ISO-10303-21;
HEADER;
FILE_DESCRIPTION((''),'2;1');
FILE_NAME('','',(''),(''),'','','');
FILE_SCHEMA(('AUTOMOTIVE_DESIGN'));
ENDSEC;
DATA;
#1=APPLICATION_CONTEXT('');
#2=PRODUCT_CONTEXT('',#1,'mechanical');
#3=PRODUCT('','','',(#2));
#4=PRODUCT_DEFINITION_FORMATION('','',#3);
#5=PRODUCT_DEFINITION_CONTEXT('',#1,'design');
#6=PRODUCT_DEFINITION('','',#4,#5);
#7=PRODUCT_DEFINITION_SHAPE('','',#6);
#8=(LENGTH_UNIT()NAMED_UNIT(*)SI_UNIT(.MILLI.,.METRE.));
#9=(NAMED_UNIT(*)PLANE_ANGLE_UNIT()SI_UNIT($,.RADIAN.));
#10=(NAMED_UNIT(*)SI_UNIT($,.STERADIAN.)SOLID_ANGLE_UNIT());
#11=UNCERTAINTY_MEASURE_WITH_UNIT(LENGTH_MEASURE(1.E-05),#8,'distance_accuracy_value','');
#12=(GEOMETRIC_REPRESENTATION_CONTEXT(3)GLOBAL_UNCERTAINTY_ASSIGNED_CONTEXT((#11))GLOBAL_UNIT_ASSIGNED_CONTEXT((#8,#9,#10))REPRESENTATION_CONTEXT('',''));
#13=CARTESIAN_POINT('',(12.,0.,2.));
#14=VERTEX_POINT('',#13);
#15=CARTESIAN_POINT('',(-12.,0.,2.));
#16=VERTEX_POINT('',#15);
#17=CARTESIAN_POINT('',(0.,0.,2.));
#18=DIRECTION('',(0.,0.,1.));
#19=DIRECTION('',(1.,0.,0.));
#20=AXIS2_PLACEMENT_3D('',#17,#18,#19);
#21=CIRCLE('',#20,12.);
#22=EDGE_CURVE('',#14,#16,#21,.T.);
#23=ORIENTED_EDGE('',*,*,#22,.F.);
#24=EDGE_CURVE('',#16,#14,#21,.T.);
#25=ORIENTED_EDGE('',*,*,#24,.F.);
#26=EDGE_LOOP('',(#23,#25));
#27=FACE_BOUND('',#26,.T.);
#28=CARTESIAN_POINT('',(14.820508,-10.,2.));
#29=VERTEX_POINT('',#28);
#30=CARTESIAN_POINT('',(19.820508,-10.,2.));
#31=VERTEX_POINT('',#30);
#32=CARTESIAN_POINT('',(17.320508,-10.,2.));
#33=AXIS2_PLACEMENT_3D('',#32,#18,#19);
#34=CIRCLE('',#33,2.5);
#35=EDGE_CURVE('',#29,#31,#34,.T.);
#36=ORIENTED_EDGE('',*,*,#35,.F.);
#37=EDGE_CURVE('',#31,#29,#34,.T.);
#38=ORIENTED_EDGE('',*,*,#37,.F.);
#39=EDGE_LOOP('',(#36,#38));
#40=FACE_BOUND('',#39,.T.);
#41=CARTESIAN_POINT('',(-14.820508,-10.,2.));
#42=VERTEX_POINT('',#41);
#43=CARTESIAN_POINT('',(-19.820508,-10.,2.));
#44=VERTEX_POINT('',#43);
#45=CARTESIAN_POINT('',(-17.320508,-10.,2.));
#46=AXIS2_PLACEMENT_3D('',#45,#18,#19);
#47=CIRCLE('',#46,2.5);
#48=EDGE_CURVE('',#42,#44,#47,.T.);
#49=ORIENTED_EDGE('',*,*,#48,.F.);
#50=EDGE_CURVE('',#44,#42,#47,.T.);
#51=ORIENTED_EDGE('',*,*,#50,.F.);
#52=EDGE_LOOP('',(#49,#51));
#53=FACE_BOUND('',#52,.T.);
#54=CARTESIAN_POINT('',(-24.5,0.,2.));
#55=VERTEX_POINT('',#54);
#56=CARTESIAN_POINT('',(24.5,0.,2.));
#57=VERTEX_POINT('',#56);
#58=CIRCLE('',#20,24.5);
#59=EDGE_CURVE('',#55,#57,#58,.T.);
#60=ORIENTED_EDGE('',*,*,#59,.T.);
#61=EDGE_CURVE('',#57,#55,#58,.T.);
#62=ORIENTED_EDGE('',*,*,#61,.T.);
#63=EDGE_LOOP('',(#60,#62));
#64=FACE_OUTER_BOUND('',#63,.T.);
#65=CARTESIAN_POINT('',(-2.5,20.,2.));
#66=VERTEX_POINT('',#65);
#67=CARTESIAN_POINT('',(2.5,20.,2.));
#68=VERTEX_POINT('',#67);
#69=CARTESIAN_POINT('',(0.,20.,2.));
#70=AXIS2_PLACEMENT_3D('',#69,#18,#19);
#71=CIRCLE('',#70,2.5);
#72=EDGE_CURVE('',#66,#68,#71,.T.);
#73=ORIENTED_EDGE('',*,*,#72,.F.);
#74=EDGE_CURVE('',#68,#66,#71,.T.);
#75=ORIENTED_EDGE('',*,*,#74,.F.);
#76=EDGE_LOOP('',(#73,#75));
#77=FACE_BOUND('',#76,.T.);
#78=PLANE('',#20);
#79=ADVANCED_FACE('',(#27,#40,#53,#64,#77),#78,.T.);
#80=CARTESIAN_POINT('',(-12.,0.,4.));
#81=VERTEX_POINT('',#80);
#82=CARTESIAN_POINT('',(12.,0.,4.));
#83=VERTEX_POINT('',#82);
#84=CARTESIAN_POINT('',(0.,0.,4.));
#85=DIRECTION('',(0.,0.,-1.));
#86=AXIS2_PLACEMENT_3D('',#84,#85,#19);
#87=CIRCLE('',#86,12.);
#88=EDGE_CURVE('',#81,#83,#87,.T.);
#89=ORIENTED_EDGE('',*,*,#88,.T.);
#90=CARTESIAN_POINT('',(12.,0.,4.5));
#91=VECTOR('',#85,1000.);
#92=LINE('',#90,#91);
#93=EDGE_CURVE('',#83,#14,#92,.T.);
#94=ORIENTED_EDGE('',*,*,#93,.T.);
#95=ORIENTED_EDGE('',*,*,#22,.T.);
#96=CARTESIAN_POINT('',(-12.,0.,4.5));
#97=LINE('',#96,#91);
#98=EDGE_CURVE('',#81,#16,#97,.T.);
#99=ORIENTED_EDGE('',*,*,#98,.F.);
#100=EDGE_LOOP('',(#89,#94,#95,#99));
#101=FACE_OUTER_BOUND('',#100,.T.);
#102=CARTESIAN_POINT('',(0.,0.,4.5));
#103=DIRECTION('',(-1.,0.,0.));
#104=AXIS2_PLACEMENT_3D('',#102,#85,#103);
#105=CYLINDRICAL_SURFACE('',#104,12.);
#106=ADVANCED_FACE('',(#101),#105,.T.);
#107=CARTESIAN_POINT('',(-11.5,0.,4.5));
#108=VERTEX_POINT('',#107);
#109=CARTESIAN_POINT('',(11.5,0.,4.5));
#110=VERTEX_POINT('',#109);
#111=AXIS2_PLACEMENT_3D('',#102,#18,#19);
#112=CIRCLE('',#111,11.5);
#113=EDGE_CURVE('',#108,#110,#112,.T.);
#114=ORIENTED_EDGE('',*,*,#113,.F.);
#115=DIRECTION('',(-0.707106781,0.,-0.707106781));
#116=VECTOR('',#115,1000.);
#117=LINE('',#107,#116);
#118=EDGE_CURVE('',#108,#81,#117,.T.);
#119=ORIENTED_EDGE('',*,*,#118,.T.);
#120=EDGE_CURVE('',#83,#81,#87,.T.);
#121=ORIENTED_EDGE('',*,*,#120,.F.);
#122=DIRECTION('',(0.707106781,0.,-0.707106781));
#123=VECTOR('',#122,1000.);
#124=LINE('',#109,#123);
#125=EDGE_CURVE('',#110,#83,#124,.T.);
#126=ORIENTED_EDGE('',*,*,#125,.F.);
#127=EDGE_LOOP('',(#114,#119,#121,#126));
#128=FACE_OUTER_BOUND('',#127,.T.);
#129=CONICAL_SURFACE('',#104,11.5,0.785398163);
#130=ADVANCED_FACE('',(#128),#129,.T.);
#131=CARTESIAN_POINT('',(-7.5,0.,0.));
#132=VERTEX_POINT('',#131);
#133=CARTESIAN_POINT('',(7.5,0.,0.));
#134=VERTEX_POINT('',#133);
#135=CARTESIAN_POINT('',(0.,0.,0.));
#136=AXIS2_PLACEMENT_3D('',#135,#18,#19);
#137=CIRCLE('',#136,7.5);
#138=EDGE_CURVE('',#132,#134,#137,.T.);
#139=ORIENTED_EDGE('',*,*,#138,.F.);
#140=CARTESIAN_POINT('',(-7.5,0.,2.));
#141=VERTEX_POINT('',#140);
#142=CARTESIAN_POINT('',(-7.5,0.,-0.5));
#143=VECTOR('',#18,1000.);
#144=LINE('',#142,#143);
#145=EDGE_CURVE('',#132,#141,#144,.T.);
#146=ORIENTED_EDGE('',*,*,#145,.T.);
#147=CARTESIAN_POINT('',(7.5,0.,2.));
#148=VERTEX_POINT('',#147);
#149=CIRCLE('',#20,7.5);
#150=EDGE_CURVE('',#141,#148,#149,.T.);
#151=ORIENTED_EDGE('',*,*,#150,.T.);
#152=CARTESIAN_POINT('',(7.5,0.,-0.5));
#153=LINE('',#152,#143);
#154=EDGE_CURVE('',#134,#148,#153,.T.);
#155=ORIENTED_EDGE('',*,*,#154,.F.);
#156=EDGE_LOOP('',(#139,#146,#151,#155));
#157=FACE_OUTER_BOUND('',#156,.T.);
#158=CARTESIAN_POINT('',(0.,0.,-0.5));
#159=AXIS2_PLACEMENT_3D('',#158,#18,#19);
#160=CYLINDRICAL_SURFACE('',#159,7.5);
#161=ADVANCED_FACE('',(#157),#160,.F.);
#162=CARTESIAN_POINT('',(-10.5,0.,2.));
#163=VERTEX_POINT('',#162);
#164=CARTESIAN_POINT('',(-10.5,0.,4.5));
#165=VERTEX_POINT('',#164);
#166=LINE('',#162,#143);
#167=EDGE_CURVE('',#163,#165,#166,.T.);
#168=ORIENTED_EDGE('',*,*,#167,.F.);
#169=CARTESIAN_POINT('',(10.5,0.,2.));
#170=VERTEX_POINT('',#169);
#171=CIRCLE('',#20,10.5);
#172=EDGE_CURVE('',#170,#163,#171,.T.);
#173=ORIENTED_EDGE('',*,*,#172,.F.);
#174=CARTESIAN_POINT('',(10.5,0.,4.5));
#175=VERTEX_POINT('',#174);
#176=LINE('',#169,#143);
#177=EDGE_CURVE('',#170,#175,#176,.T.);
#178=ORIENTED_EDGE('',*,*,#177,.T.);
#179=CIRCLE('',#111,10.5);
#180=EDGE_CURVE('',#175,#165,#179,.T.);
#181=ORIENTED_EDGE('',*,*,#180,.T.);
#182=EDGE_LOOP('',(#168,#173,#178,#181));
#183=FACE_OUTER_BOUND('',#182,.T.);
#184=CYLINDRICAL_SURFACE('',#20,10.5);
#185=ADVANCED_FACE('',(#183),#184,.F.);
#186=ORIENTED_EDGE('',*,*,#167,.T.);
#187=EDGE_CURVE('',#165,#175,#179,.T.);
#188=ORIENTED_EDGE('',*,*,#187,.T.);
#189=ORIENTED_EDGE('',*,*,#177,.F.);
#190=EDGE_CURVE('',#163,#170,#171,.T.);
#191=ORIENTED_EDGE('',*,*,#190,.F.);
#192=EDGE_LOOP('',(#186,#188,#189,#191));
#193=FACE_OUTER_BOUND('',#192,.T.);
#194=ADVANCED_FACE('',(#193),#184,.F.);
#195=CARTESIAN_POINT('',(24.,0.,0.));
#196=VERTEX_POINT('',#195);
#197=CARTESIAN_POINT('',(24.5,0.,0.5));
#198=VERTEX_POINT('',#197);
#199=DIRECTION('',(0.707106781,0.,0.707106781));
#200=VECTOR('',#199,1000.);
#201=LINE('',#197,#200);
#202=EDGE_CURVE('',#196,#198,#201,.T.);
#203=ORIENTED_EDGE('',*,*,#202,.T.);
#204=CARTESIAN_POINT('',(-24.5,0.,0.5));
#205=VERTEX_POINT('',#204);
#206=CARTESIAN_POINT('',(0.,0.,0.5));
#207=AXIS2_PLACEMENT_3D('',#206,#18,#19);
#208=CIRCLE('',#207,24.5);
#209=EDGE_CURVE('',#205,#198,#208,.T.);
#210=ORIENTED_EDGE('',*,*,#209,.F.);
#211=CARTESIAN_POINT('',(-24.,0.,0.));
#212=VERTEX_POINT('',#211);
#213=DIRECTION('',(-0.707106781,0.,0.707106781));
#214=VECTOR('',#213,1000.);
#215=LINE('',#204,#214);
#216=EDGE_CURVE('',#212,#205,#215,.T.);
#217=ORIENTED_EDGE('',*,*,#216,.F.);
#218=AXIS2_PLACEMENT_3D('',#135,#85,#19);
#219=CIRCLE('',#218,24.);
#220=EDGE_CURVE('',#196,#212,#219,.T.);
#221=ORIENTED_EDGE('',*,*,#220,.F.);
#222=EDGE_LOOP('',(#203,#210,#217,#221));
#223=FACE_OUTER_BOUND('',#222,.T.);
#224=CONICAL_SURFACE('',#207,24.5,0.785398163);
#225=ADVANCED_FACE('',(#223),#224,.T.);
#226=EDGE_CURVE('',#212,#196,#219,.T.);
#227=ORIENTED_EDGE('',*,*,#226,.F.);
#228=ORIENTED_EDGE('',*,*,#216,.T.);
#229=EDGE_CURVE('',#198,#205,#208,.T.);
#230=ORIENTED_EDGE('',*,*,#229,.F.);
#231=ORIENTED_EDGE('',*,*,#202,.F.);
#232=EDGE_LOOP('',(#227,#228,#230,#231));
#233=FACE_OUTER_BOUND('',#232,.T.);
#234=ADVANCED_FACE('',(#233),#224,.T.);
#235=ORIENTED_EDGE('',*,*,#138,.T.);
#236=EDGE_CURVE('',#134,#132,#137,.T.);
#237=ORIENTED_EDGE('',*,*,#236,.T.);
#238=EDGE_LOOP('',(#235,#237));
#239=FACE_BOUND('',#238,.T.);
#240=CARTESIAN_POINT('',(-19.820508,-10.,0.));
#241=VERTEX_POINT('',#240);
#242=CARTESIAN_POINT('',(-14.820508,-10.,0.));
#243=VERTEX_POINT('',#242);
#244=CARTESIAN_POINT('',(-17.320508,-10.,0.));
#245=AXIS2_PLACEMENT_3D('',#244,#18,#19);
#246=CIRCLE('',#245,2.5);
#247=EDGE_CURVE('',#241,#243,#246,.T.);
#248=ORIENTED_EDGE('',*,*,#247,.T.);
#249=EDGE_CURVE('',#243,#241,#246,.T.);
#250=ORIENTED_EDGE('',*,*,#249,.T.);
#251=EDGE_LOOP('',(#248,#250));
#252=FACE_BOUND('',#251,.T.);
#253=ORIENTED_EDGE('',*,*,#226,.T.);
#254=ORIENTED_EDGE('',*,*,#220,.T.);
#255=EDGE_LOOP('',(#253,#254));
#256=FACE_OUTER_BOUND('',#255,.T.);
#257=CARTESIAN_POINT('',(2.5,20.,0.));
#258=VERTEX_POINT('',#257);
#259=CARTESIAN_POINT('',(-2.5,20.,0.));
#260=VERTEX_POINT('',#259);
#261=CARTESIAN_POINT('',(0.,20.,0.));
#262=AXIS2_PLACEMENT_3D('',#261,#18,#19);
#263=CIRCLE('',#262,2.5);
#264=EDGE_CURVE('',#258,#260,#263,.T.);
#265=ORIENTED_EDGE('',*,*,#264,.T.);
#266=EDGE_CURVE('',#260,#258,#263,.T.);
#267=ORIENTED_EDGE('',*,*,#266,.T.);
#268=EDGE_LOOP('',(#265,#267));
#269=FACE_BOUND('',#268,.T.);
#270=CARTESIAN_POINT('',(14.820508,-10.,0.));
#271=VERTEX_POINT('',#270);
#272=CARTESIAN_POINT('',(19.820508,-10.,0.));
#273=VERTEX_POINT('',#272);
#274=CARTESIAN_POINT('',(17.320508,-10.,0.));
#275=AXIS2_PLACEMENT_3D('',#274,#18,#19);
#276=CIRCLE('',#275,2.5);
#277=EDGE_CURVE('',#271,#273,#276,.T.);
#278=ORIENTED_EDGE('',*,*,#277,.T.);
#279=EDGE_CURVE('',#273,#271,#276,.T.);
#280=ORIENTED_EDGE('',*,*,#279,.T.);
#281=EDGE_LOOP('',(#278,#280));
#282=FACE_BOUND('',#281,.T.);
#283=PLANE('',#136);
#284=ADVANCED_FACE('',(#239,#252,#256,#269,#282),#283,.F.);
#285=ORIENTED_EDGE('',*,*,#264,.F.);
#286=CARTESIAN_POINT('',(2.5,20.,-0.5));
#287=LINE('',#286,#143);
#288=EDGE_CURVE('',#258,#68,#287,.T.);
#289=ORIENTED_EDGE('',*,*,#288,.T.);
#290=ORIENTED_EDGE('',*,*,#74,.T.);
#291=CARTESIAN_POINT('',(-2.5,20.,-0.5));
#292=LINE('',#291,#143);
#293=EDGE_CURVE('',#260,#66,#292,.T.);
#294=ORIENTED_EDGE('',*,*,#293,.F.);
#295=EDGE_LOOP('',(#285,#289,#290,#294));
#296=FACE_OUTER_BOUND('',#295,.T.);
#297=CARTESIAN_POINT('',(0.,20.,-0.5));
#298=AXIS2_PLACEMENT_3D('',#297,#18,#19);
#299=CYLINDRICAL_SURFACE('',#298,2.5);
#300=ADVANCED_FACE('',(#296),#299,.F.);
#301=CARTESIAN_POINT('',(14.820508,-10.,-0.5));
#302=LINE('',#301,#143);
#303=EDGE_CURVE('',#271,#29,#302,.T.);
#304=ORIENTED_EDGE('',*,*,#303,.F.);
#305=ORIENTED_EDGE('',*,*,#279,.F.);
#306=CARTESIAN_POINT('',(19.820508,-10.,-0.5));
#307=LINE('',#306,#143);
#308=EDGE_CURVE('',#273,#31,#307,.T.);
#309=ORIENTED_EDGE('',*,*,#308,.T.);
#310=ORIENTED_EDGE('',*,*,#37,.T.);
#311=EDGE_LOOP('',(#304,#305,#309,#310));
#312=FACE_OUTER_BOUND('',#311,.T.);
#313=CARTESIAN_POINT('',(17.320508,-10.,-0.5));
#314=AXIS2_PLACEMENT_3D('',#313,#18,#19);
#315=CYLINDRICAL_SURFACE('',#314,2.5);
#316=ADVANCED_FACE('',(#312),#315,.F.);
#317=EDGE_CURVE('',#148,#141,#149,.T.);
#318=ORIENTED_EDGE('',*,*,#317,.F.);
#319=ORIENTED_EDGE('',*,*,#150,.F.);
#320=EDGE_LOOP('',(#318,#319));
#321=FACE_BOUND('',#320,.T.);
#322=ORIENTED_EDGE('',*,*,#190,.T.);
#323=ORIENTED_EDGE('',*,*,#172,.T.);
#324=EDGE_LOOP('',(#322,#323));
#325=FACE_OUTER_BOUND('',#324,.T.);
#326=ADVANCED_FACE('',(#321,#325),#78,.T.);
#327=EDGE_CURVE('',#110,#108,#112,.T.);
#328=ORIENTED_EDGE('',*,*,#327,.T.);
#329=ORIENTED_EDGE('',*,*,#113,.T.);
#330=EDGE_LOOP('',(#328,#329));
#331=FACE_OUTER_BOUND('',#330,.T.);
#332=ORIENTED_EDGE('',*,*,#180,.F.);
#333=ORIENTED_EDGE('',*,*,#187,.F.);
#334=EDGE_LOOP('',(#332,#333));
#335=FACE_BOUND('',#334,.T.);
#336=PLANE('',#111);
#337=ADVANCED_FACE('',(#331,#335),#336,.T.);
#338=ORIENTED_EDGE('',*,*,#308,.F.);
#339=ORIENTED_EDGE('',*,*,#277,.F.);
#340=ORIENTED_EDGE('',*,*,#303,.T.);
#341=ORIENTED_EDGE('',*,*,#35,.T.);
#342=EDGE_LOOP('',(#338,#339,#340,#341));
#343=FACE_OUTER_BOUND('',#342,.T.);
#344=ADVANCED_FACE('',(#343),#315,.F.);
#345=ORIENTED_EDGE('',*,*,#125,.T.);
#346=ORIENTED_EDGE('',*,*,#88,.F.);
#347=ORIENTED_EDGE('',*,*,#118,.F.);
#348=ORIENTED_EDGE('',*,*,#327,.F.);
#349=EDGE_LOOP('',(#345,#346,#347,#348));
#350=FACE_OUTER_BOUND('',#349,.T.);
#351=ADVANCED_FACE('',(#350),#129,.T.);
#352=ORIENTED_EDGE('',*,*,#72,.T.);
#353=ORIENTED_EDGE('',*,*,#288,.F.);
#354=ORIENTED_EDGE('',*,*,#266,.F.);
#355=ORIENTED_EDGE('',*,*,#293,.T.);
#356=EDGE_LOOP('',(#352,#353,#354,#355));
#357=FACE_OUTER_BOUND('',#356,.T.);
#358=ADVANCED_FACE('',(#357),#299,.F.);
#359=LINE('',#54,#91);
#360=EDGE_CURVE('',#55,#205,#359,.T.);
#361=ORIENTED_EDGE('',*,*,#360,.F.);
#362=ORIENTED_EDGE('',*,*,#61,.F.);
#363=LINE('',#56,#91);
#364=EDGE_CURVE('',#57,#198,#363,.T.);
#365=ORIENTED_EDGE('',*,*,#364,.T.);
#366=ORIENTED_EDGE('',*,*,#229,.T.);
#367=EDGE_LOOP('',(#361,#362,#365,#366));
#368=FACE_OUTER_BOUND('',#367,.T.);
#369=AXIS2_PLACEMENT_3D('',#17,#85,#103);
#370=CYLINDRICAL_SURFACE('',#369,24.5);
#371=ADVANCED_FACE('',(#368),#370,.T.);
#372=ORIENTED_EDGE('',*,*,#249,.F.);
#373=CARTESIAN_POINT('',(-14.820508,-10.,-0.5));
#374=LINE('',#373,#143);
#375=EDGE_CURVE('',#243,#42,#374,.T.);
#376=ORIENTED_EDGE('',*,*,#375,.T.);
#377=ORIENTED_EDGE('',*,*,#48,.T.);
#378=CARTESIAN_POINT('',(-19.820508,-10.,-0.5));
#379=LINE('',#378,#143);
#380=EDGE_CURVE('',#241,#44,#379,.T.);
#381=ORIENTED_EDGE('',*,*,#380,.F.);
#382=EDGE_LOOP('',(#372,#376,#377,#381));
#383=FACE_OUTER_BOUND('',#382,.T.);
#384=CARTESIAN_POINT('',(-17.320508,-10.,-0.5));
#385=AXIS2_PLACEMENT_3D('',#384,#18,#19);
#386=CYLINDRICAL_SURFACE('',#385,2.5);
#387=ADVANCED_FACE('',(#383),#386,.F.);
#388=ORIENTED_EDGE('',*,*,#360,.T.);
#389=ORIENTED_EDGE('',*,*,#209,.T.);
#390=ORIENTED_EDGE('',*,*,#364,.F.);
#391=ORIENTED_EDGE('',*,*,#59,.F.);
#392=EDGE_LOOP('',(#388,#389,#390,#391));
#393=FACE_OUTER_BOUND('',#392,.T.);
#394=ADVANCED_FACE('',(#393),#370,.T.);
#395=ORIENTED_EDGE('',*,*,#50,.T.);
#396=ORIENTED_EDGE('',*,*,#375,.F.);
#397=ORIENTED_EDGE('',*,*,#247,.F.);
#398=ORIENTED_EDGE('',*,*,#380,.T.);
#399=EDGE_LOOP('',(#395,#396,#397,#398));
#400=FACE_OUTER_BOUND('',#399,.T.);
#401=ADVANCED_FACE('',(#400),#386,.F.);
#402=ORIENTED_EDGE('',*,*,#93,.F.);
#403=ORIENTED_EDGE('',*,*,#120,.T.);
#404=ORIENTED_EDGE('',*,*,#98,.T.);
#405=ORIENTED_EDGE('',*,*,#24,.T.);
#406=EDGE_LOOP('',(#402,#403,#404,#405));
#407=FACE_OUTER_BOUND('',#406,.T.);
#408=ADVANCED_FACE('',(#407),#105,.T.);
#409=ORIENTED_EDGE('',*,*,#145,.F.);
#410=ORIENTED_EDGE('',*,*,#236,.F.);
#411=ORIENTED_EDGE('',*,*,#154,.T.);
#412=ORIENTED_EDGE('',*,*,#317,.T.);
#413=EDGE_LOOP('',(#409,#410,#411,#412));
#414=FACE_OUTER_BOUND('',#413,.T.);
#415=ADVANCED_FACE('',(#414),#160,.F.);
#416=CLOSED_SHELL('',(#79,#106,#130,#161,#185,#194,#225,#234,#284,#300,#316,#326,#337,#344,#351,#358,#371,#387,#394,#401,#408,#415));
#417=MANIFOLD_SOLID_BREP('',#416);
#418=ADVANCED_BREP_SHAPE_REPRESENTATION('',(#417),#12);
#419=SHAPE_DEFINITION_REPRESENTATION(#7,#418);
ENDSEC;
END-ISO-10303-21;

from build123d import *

# Parameters (mm, degrees)
SKETCH1_R           = 24.5
BOSS_EXTRUDE1_DEPTH = 2
SKETCH2_R           = 12
BOSS_EXTRUDE2_DEPTH = 2.5
CUT_EXTRUDE1_START  = 2.5
SKETCH3_R           = 10.5
CUT_EXTRUDE1_DEPTH  = 2.5
SKETCH4_R           = 7.5
CUT_EXTRUDE2_DEPTH  = 2.5
SKETCH5_R           = 2.5
CUT_EXTRUDE3_DEPTH  = 2.5
CHAMFER1_SIZE       = 0.5


with BuildPart() as part:
    # Sketch1 → Boss-Extrude1 (new body)
    with BuildSketch(Plane.XY):
        Circle(SKETCH1_R)
    extrude(amount=BOSS_EXTRUDE1_DEPTH)

    # Sketch2 → Boss-Extrude2 (add)
    with BuildSketch(Plane.XY.offset(2)):
        Circle(SKETCH2_R)
    extrude(amount=BOSS_EXTRUDE2_DEPTH)

    # Sketch3 → Cut-Extrude1 (cut)
    with BuildSketch(Plane.XY.offset(2).offset(CUT_EXTRUDE1_START)):
        Circle(SKETCH3_R)
    extrude(amount=-CUT_EXTRUDE1_DEPTH, mode=Mode.SUBTRACT)

    # Sketch4 → Cut-Extrude2 (cut)
    with BuildSketch(Plane.XY.offset(2)):
        Circle(SKETCH4_R)
    extrude(amount=-CUT_EXTRUDE2_DEPTH, mode=Mode.SUBTRACT)

    # Sketch5 → Cut-Extrude3 (cut)
    with BuildSketch(Plane.XY.offset(2)):
        with Locations((0, 20)):
            Circle(SKETCH5_R)
        with Locations((17.320508076, -10)):
            Circle(SKETCH5_R)
        with Locations((-17.320508076, -10)):
            Circle(SKETCH5_R)
    extrude(amount=-CUT_EXTRUDE3_DEPTH, mode=Mode.SUBTRACT)

    # Chamfer1
    chamfer1_edges = [part.edges().sort_by_distance(p)[0] for p in [
        (-24.5, 0, 0),
        (-12, 0, 4.5),
    ]]
    chamfer(chamfer1_edges, length=CHAMFER1_SIZE)


solid = part.part
